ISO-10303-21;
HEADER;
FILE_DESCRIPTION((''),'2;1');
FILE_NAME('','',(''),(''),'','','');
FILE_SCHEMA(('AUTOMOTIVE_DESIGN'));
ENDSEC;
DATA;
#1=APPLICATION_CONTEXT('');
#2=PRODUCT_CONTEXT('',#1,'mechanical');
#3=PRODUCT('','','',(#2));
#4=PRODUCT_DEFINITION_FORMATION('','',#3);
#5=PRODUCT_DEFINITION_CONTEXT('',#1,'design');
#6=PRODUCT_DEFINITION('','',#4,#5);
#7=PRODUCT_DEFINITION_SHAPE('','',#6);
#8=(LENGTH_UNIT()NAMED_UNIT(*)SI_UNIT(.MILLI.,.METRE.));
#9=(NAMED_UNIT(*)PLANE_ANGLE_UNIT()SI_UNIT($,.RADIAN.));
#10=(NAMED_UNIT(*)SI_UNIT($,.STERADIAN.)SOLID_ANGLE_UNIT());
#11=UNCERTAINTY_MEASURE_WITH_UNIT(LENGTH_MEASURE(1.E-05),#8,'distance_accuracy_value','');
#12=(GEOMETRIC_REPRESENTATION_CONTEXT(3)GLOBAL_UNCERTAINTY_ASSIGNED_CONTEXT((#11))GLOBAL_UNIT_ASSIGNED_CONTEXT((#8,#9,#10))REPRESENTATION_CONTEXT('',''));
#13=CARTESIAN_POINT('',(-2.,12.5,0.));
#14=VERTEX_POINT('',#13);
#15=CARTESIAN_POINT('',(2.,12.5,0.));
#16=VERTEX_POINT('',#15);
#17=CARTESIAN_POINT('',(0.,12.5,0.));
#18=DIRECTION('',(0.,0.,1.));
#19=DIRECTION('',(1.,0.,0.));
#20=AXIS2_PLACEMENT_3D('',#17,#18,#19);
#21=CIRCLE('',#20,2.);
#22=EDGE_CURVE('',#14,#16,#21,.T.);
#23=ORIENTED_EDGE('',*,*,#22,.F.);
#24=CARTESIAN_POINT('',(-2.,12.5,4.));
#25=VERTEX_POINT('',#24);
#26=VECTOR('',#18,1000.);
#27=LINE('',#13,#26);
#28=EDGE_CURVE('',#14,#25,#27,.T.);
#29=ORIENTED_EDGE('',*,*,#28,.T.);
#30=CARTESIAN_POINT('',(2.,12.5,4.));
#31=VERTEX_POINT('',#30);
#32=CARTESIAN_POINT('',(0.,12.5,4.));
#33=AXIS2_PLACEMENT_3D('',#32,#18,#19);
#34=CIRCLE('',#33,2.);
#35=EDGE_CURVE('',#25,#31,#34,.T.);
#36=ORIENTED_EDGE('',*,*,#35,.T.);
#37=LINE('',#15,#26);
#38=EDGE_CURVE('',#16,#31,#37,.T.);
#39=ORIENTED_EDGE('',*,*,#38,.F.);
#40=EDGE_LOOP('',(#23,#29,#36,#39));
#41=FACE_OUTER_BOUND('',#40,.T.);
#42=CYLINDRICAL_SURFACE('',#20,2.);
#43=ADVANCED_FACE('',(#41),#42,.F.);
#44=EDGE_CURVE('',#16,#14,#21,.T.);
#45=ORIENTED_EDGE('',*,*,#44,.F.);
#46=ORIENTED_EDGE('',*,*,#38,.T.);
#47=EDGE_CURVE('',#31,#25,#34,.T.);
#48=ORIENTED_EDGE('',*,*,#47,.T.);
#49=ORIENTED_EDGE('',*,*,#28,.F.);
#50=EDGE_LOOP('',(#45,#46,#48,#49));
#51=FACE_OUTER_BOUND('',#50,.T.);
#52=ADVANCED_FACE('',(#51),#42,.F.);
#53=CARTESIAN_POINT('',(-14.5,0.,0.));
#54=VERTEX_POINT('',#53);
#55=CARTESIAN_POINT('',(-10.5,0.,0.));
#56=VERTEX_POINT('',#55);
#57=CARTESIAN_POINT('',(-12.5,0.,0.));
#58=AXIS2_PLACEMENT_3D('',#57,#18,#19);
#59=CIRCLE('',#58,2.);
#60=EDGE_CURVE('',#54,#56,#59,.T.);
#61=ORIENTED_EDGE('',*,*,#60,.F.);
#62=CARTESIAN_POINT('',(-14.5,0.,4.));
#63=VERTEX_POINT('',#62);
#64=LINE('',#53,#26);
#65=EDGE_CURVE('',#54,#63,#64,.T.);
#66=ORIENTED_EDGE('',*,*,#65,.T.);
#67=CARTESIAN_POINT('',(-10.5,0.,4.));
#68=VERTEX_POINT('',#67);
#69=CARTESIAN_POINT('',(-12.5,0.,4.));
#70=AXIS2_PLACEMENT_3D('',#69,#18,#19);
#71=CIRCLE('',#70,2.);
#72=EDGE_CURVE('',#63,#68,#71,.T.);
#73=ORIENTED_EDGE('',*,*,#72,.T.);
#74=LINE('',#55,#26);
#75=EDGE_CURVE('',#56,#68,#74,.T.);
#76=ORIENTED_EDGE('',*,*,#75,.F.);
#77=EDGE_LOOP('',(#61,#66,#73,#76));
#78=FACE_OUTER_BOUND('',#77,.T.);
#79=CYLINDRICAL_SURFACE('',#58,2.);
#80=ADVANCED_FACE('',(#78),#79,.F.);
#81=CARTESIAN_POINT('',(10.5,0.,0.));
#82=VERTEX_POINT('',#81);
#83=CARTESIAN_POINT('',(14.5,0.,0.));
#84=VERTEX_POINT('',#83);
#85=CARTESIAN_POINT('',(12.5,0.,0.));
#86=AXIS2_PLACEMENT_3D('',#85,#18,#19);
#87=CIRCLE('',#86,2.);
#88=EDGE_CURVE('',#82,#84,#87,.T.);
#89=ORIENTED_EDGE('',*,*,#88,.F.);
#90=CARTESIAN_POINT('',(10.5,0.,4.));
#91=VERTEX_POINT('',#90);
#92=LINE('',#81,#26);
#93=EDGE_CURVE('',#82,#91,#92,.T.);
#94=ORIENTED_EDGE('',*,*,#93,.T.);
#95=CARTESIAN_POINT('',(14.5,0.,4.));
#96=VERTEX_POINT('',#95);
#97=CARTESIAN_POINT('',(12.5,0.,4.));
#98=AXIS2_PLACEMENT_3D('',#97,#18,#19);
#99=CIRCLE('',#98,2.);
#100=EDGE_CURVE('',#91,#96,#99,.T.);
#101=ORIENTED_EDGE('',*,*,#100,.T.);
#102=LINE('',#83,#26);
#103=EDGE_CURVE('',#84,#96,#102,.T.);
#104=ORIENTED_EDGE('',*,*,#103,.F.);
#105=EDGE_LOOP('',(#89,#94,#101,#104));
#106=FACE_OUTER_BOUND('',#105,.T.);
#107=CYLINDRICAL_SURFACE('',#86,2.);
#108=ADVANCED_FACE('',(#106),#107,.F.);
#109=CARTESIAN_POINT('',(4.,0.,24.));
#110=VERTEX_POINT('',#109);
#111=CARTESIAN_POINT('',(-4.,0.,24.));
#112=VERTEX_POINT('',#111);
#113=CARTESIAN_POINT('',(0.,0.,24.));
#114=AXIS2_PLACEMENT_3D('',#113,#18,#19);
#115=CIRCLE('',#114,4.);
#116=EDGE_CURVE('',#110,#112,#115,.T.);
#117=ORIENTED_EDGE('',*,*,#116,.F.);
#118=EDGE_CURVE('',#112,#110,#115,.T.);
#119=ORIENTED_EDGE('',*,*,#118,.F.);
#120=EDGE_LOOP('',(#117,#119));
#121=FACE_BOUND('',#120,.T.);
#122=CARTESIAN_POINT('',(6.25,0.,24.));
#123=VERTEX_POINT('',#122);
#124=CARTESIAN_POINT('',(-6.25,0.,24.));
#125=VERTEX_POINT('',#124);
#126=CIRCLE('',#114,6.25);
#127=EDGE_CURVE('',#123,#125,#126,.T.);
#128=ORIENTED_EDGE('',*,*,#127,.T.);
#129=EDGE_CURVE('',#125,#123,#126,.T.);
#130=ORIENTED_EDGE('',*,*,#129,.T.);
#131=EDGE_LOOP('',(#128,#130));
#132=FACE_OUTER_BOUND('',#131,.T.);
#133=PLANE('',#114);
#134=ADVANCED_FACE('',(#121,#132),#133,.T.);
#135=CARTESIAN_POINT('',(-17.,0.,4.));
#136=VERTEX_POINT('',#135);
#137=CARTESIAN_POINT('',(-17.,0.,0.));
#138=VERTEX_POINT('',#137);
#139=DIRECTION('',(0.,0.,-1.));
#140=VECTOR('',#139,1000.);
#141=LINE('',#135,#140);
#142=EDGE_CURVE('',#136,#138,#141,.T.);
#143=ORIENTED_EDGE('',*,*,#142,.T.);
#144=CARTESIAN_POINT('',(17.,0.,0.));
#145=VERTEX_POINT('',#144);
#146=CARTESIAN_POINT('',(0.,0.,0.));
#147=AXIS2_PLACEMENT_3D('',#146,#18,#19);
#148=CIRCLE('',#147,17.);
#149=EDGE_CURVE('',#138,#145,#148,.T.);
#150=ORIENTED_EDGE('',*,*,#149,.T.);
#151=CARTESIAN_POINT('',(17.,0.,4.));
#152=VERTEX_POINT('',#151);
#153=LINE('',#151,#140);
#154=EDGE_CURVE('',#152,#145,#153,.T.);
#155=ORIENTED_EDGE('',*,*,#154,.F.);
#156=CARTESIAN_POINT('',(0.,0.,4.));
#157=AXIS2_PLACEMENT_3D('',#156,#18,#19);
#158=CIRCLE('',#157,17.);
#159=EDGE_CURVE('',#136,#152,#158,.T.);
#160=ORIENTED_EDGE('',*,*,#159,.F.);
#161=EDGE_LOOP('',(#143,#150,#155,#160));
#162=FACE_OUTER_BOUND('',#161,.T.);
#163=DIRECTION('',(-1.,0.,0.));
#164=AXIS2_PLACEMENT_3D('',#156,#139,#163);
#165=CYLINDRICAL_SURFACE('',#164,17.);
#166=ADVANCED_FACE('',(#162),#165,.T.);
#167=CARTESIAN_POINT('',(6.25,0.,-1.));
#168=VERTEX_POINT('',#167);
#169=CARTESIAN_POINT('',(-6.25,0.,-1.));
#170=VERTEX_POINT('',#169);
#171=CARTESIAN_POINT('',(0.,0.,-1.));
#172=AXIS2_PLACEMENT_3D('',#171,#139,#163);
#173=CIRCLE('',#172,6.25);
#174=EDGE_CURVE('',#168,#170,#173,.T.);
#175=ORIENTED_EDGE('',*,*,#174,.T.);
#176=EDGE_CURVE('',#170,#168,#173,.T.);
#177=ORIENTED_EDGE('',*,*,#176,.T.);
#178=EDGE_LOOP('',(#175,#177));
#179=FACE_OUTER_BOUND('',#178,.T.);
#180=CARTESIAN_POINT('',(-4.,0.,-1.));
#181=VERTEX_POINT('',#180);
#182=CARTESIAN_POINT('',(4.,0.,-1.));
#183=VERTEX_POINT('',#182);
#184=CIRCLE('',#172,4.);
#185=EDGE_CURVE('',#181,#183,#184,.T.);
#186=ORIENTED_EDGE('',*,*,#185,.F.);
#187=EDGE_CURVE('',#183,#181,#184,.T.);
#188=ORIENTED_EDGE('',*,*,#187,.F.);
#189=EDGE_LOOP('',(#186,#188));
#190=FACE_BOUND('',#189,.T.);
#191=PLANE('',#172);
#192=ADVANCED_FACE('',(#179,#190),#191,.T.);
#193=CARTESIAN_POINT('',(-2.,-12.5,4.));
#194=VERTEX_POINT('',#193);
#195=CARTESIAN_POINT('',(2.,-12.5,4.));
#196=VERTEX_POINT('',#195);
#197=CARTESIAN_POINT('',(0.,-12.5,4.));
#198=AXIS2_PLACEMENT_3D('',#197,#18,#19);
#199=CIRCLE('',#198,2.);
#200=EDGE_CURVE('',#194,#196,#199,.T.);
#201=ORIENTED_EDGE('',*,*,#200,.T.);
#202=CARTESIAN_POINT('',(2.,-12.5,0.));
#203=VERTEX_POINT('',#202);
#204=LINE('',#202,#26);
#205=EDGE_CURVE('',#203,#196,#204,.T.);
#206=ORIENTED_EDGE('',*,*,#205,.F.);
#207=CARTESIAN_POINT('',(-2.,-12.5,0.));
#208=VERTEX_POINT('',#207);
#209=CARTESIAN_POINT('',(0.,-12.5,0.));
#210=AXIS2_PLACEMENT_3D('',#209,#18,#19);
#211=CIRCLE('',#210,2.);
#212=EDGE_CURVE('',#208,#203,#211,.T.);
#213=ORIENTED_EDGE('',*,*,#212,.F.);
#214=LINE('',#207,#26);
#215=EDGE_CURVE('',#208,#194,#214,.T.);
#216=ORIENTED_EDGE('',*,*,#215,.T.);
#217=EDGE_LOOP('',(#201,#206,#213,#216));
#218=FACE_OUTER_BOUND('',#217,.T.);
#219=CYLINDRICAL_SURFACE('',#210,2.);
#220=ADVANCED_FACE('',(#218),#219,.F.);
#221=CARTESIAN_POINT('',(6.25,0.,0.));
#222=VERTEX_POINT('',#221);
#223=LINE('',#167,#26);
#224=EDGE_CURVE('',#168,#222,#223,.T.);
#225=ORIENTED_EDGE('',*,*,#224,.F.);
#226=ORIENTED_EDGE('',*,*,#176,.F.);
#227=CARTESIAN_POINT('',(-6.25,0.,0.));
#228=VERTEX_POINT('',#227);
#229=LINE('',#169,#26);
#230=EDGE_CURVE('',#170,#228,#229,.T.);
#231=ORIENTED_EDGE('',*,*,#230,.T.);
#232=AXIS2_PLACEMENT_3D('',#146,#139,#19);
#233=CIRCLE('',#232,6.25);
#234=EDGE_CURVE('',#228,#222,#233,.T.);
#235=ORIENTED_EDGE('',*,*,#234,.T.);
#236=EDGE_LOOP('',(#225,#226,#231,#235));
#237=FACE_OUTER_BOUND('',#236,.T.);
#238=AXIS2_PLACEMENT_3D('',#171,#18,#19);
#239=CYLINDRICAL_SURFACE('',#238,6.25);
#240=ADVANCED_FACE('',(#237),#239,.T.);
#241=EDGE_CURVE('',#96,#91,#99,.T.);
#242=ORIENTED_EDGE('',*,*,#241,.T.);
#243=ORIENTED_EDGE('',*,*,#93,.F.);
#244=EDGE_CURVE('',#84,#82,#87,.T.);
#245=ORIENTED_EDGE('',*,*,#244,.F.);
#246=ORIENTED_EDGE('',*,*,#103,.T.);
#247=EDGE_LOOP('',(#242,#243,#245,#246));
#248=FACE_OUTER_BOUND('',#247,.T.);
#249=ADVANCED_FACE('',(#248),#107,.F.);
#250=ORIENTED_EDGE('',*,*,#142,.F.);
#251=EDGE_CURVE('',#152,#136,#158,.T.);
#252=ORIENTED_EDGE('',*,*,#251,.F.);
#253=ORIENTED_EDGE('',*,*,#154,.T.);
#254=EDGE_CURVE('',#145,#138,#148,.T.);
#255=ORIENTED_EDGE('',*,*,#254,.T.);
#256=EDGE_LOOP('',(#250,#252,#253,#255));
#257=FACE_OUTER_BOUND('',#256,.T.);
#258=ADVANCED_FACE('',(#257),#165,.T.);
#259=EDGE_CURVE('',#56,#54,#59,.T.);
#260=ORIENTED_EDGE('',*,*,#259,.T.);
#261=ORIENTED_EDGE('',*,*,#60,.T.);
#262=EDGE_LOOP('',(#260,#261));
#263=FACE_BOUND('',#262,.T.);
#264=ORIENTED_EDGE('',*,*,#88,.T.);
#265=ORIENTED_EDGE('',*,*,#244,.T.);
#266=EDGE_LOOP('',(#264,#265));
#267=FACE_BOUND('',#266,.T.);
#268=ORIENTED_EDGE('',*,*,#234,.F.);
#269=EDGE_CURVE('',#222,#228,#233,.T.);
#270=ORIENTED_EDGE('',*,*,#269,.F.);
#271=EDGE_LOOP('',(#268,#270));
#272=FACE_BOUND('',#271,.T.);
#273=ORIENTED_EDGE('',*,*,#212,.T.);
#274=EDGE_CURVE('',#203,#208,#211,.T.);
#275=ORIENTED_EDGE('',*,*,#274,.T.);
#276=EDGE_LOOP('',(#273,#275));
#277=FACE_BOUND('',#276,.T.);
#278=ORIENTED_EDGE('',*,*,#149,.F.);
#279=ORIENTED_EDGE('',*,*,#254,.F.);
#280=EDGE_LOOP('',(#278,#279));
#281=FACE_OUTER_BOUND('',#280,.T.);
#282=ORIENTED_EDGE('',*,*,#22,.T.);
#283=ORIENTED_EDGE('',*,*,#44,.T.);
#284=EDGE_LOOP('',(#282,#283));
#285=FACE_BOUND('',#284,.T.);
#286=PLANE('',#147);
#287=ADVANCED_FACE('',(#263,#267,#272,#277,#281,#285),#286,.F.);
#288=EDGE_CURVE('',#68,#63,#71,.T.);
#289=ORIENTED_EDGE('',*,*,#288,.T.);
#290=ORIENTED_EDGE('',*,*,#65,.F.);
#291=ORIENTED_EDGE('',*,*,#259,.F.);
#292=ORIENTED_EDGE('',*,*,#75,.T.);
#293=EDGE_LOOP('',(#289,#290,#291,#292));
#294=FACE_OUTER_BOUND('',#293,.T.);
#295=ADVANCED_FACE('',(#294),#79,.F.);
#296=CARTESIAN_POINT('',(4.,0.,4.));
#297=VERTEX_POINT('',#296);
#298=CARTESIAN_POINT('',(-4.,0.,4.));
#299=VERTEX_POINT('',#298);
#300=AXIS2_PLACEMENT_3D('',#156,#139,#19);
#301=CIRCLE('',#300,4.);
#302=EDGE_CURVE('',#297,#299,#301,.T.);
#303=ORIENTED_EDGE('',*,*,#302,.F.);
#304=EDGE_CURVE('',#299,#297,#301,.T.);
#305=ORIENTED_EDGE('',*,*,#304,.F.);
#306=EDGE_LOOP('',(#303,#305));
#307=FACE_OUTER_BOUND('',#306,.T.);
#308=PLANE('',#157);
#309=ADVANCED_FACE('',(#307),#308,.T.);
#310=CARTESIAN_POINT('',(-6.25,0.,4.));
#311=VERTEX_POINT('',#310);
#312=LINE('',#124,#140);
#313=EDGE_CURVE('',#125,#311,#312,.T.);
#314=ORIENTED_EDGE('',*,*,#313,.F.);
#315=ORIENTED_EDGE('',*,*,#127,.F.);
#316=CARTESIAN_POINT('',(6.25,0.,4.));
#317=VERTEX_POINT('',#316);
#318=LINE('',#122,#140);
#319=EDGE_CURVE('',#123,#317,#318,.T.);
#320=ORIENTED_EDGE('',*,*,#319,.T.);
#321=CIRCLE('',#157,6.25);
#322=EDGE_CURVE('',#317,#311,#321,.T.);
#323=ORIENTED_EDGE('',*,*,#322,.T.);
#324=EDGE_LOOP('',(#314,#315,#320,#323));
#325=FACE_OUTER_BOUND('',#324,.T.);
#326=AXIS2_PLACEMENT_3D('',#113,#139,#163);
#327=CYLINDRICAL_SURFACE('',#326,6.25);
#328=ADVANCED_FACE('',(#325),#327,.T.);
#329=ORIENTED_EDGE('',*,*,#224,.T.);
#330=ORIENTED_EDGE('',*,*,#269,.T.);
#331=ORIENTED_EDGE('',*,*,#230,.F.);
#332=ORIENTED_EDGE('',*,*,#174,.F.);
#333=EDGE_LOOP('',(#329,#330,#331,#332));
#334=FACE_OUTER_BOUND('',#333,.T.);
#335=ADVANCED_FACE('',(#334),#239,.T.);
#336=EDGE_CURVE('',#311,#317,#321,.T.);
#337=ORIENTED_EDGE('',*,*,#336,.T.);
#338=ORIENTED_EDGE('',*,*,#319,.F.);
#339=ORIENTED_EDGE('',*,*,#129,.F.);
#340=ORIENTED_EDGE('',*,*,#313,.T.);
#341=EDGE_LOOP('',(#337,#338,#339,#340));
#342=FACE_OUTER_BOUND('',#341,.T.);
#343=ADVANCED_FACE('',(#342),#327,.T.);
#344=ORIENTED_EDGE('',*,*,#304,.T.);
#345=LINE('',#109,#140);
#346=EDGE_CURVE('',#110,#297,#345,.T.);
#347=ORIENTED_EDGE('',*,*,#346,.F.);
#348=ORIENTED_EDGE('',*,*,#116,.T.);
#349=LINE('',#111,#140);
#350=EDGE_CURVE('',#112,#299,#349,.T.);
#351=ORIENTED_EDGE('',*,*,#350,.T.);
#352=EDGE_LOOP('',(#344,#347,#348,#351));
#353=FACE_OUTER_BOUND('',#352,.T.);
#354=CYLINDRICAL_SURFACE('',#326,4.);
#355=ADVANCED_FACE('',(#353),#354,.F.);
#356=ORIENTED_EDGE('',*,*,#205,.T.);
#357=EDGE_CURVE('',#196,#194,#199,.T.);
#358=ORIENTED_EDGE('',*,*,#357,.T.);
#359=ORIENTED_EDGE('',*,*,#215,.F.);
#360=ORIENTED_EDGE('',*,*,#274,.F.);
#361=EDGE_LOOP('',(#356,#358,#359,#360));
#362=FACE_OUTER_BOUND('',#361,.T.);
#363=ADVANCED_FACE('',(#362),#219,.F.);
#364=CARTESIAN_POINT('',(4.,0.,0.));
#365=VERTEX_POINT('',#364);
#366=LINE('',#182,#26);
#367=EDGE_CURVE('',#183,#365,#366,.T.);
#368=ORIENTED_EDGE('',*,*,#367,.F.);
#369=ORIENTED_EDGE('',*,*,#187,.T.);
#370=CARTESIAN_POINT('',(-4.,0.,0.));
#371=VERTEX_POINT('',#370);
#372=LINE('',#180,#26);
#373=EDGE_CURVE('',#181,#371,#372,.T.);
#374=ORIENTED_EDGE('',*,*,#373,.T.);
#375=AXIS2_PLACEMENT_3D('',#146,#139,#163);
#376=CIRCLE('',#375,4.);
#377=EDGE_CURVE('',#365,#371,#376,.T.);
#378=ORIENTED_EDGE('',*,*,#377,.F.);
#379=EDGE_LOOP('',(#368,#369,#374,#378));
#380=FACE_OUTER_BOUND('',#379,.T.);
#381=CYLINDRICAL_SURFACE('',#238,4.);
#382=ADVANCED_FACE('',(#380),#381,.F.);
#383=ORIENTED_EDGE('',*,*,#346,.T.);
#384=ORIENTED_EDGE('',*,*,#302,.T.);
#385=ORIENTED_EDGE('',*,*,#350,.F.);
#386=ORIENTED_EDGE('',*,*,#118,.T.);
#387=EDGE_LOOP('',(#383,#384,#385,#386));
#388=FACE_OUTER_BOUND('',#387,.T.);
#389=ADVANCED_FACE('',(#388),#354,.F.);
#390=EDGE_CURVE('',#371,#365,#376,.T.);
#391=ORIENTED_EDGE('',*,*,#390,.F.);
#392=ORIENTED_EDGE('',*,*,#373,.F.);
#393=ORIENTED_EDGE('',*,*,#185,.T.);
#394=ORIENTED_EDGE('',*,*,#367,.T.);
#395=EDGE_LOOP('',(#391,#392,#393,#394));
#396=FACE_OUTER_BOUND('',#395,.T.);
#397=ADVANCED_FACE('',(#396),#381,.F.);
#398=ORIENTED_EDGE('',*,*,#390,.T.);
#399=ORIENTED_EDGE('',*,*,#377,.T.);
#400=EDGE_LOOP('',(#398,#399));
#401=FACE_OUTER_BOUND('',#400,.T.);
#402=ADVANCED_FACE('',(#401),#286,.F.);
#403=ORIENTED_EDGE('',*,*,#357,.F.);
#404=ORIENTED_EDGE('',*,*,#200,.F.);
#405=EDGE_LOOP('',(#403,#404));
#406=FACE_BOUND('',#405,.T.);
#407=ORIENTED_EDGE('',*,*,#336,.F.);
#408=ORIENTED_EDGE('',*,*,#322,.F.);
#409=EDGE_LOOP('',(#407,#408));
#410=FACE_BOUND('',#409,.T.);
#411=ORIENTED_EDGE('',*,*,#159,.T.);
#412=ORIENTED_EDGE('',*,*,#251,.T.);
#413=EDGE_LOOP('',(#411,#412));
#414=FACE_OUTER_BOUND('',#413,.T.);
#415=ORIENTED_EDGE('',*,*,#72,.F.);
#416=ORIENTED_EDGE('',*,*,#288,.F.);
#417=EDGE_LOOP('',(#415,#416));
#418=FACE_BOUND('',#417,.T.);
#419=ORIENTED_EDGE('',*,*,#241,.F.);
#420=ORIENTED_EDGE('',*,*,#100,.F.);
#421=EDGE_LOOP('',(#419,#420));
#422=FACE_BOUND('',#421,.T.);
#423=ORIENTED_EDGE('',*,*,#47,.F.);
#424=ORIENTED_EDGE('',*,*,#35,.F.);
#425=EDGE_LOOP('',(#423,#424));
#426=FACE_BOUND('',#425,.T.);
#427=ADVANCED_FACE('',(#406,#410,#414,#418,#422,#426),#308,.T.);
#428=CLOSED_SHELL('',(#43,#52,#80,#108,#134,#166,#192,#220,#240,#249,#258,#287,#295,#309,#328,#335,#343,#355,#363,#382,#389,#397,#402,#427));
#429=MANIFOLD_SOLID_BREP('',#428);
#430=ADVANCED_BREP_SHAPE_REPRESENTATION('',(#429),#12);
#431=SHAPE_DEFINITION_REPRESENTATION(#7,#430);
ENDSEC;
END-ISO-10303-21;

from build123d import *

# Parameters (mm, degrees)
FLANGE_PROFILE_SKETCH_R = 17
FLANGE_34X4_DEPTH       = 4
HUB_PROFILE_SKETCH_R    = 6.25
HUB_PROFILE_SKETCH_R_2  = 4
HUB_TUBE_20MM_DEPTH     = 20
BOLT_HOLES_SKETCH_R     = 2
BOLT_HOLES_4X_DEPTH     = 4
REAR_START              = 1
REAR_SPIGOT_SKETCH_R    = 6.25
REAR_SPIGOT_SKETCH_R_2  = 4
REAR_SPIGOT_1MM_DEPTH   = 1


with BuildPart() as part:
    # Flange Profile Sketch → Flange Ø34x4 (new body)
    with BuildSketch(Plane.XY):
        Circle(FLANGE_PROFILE_SKETCH_R)
    extrude(amount=FLANGE_34X4_DEPTH)

    # Hub Profile Sketch → Hub Tube 20mm (add)
    with BuildSketch(Plane.XY.offset(4)):
        Circle(HUB_PROFILE_SKETCH_R)
        Circle(HUB_PROFILE_SKETCH_R_2, mode=Mode.SUBTRACT)
    extrude(amount=HUB_TUBE_20MM_DEPTH)

    # Bolt Holes Sketch → Bolt Holes 4x (cut)
    with BuildSketch(Plane.XY.offset(4)):
        with Locations((0, 12.5)):
            Circle(BOLT_HOLES_SKETCH_R)
        with Locations((12.5, 0)):
            Circle(BOLT_HOLES_SKETCH_R)
        with Locations((0, -12.5)):
            Circle(BOLT_HOLES_SKETCH_R)
        with Locations((-12.5, 0)):
            Circle(BOLT_HOLES_SKETCH_R)
    extrude(amount=-BOLT_HOLES_4X_DEPTH, mode=Mode.SUBTRACT)

    # Rear Spigot Sketch → Rear Spigot 1mm (add)
    with BuildSketch(Plane(origin=(0, 0, 0), x_dir=(-1, 0, 0), z_dir=(0, 0, -1)).offset(REAR_START)):
        with Locations(Location((0, 0, 0), (0, 0, 180))):
            Circle(REAR_SPIGOT_SKETCH_R)
        with Locations(Location((0, 0, 0), (0, 0, 180))):
            Circle(REAR_SPIGOT_SKETCH_R_2, mode=Mode.SUBTRACT)
    extrude(amount=-REAR_SPIGOT_1MM_DEPTH)


solid = part.part
